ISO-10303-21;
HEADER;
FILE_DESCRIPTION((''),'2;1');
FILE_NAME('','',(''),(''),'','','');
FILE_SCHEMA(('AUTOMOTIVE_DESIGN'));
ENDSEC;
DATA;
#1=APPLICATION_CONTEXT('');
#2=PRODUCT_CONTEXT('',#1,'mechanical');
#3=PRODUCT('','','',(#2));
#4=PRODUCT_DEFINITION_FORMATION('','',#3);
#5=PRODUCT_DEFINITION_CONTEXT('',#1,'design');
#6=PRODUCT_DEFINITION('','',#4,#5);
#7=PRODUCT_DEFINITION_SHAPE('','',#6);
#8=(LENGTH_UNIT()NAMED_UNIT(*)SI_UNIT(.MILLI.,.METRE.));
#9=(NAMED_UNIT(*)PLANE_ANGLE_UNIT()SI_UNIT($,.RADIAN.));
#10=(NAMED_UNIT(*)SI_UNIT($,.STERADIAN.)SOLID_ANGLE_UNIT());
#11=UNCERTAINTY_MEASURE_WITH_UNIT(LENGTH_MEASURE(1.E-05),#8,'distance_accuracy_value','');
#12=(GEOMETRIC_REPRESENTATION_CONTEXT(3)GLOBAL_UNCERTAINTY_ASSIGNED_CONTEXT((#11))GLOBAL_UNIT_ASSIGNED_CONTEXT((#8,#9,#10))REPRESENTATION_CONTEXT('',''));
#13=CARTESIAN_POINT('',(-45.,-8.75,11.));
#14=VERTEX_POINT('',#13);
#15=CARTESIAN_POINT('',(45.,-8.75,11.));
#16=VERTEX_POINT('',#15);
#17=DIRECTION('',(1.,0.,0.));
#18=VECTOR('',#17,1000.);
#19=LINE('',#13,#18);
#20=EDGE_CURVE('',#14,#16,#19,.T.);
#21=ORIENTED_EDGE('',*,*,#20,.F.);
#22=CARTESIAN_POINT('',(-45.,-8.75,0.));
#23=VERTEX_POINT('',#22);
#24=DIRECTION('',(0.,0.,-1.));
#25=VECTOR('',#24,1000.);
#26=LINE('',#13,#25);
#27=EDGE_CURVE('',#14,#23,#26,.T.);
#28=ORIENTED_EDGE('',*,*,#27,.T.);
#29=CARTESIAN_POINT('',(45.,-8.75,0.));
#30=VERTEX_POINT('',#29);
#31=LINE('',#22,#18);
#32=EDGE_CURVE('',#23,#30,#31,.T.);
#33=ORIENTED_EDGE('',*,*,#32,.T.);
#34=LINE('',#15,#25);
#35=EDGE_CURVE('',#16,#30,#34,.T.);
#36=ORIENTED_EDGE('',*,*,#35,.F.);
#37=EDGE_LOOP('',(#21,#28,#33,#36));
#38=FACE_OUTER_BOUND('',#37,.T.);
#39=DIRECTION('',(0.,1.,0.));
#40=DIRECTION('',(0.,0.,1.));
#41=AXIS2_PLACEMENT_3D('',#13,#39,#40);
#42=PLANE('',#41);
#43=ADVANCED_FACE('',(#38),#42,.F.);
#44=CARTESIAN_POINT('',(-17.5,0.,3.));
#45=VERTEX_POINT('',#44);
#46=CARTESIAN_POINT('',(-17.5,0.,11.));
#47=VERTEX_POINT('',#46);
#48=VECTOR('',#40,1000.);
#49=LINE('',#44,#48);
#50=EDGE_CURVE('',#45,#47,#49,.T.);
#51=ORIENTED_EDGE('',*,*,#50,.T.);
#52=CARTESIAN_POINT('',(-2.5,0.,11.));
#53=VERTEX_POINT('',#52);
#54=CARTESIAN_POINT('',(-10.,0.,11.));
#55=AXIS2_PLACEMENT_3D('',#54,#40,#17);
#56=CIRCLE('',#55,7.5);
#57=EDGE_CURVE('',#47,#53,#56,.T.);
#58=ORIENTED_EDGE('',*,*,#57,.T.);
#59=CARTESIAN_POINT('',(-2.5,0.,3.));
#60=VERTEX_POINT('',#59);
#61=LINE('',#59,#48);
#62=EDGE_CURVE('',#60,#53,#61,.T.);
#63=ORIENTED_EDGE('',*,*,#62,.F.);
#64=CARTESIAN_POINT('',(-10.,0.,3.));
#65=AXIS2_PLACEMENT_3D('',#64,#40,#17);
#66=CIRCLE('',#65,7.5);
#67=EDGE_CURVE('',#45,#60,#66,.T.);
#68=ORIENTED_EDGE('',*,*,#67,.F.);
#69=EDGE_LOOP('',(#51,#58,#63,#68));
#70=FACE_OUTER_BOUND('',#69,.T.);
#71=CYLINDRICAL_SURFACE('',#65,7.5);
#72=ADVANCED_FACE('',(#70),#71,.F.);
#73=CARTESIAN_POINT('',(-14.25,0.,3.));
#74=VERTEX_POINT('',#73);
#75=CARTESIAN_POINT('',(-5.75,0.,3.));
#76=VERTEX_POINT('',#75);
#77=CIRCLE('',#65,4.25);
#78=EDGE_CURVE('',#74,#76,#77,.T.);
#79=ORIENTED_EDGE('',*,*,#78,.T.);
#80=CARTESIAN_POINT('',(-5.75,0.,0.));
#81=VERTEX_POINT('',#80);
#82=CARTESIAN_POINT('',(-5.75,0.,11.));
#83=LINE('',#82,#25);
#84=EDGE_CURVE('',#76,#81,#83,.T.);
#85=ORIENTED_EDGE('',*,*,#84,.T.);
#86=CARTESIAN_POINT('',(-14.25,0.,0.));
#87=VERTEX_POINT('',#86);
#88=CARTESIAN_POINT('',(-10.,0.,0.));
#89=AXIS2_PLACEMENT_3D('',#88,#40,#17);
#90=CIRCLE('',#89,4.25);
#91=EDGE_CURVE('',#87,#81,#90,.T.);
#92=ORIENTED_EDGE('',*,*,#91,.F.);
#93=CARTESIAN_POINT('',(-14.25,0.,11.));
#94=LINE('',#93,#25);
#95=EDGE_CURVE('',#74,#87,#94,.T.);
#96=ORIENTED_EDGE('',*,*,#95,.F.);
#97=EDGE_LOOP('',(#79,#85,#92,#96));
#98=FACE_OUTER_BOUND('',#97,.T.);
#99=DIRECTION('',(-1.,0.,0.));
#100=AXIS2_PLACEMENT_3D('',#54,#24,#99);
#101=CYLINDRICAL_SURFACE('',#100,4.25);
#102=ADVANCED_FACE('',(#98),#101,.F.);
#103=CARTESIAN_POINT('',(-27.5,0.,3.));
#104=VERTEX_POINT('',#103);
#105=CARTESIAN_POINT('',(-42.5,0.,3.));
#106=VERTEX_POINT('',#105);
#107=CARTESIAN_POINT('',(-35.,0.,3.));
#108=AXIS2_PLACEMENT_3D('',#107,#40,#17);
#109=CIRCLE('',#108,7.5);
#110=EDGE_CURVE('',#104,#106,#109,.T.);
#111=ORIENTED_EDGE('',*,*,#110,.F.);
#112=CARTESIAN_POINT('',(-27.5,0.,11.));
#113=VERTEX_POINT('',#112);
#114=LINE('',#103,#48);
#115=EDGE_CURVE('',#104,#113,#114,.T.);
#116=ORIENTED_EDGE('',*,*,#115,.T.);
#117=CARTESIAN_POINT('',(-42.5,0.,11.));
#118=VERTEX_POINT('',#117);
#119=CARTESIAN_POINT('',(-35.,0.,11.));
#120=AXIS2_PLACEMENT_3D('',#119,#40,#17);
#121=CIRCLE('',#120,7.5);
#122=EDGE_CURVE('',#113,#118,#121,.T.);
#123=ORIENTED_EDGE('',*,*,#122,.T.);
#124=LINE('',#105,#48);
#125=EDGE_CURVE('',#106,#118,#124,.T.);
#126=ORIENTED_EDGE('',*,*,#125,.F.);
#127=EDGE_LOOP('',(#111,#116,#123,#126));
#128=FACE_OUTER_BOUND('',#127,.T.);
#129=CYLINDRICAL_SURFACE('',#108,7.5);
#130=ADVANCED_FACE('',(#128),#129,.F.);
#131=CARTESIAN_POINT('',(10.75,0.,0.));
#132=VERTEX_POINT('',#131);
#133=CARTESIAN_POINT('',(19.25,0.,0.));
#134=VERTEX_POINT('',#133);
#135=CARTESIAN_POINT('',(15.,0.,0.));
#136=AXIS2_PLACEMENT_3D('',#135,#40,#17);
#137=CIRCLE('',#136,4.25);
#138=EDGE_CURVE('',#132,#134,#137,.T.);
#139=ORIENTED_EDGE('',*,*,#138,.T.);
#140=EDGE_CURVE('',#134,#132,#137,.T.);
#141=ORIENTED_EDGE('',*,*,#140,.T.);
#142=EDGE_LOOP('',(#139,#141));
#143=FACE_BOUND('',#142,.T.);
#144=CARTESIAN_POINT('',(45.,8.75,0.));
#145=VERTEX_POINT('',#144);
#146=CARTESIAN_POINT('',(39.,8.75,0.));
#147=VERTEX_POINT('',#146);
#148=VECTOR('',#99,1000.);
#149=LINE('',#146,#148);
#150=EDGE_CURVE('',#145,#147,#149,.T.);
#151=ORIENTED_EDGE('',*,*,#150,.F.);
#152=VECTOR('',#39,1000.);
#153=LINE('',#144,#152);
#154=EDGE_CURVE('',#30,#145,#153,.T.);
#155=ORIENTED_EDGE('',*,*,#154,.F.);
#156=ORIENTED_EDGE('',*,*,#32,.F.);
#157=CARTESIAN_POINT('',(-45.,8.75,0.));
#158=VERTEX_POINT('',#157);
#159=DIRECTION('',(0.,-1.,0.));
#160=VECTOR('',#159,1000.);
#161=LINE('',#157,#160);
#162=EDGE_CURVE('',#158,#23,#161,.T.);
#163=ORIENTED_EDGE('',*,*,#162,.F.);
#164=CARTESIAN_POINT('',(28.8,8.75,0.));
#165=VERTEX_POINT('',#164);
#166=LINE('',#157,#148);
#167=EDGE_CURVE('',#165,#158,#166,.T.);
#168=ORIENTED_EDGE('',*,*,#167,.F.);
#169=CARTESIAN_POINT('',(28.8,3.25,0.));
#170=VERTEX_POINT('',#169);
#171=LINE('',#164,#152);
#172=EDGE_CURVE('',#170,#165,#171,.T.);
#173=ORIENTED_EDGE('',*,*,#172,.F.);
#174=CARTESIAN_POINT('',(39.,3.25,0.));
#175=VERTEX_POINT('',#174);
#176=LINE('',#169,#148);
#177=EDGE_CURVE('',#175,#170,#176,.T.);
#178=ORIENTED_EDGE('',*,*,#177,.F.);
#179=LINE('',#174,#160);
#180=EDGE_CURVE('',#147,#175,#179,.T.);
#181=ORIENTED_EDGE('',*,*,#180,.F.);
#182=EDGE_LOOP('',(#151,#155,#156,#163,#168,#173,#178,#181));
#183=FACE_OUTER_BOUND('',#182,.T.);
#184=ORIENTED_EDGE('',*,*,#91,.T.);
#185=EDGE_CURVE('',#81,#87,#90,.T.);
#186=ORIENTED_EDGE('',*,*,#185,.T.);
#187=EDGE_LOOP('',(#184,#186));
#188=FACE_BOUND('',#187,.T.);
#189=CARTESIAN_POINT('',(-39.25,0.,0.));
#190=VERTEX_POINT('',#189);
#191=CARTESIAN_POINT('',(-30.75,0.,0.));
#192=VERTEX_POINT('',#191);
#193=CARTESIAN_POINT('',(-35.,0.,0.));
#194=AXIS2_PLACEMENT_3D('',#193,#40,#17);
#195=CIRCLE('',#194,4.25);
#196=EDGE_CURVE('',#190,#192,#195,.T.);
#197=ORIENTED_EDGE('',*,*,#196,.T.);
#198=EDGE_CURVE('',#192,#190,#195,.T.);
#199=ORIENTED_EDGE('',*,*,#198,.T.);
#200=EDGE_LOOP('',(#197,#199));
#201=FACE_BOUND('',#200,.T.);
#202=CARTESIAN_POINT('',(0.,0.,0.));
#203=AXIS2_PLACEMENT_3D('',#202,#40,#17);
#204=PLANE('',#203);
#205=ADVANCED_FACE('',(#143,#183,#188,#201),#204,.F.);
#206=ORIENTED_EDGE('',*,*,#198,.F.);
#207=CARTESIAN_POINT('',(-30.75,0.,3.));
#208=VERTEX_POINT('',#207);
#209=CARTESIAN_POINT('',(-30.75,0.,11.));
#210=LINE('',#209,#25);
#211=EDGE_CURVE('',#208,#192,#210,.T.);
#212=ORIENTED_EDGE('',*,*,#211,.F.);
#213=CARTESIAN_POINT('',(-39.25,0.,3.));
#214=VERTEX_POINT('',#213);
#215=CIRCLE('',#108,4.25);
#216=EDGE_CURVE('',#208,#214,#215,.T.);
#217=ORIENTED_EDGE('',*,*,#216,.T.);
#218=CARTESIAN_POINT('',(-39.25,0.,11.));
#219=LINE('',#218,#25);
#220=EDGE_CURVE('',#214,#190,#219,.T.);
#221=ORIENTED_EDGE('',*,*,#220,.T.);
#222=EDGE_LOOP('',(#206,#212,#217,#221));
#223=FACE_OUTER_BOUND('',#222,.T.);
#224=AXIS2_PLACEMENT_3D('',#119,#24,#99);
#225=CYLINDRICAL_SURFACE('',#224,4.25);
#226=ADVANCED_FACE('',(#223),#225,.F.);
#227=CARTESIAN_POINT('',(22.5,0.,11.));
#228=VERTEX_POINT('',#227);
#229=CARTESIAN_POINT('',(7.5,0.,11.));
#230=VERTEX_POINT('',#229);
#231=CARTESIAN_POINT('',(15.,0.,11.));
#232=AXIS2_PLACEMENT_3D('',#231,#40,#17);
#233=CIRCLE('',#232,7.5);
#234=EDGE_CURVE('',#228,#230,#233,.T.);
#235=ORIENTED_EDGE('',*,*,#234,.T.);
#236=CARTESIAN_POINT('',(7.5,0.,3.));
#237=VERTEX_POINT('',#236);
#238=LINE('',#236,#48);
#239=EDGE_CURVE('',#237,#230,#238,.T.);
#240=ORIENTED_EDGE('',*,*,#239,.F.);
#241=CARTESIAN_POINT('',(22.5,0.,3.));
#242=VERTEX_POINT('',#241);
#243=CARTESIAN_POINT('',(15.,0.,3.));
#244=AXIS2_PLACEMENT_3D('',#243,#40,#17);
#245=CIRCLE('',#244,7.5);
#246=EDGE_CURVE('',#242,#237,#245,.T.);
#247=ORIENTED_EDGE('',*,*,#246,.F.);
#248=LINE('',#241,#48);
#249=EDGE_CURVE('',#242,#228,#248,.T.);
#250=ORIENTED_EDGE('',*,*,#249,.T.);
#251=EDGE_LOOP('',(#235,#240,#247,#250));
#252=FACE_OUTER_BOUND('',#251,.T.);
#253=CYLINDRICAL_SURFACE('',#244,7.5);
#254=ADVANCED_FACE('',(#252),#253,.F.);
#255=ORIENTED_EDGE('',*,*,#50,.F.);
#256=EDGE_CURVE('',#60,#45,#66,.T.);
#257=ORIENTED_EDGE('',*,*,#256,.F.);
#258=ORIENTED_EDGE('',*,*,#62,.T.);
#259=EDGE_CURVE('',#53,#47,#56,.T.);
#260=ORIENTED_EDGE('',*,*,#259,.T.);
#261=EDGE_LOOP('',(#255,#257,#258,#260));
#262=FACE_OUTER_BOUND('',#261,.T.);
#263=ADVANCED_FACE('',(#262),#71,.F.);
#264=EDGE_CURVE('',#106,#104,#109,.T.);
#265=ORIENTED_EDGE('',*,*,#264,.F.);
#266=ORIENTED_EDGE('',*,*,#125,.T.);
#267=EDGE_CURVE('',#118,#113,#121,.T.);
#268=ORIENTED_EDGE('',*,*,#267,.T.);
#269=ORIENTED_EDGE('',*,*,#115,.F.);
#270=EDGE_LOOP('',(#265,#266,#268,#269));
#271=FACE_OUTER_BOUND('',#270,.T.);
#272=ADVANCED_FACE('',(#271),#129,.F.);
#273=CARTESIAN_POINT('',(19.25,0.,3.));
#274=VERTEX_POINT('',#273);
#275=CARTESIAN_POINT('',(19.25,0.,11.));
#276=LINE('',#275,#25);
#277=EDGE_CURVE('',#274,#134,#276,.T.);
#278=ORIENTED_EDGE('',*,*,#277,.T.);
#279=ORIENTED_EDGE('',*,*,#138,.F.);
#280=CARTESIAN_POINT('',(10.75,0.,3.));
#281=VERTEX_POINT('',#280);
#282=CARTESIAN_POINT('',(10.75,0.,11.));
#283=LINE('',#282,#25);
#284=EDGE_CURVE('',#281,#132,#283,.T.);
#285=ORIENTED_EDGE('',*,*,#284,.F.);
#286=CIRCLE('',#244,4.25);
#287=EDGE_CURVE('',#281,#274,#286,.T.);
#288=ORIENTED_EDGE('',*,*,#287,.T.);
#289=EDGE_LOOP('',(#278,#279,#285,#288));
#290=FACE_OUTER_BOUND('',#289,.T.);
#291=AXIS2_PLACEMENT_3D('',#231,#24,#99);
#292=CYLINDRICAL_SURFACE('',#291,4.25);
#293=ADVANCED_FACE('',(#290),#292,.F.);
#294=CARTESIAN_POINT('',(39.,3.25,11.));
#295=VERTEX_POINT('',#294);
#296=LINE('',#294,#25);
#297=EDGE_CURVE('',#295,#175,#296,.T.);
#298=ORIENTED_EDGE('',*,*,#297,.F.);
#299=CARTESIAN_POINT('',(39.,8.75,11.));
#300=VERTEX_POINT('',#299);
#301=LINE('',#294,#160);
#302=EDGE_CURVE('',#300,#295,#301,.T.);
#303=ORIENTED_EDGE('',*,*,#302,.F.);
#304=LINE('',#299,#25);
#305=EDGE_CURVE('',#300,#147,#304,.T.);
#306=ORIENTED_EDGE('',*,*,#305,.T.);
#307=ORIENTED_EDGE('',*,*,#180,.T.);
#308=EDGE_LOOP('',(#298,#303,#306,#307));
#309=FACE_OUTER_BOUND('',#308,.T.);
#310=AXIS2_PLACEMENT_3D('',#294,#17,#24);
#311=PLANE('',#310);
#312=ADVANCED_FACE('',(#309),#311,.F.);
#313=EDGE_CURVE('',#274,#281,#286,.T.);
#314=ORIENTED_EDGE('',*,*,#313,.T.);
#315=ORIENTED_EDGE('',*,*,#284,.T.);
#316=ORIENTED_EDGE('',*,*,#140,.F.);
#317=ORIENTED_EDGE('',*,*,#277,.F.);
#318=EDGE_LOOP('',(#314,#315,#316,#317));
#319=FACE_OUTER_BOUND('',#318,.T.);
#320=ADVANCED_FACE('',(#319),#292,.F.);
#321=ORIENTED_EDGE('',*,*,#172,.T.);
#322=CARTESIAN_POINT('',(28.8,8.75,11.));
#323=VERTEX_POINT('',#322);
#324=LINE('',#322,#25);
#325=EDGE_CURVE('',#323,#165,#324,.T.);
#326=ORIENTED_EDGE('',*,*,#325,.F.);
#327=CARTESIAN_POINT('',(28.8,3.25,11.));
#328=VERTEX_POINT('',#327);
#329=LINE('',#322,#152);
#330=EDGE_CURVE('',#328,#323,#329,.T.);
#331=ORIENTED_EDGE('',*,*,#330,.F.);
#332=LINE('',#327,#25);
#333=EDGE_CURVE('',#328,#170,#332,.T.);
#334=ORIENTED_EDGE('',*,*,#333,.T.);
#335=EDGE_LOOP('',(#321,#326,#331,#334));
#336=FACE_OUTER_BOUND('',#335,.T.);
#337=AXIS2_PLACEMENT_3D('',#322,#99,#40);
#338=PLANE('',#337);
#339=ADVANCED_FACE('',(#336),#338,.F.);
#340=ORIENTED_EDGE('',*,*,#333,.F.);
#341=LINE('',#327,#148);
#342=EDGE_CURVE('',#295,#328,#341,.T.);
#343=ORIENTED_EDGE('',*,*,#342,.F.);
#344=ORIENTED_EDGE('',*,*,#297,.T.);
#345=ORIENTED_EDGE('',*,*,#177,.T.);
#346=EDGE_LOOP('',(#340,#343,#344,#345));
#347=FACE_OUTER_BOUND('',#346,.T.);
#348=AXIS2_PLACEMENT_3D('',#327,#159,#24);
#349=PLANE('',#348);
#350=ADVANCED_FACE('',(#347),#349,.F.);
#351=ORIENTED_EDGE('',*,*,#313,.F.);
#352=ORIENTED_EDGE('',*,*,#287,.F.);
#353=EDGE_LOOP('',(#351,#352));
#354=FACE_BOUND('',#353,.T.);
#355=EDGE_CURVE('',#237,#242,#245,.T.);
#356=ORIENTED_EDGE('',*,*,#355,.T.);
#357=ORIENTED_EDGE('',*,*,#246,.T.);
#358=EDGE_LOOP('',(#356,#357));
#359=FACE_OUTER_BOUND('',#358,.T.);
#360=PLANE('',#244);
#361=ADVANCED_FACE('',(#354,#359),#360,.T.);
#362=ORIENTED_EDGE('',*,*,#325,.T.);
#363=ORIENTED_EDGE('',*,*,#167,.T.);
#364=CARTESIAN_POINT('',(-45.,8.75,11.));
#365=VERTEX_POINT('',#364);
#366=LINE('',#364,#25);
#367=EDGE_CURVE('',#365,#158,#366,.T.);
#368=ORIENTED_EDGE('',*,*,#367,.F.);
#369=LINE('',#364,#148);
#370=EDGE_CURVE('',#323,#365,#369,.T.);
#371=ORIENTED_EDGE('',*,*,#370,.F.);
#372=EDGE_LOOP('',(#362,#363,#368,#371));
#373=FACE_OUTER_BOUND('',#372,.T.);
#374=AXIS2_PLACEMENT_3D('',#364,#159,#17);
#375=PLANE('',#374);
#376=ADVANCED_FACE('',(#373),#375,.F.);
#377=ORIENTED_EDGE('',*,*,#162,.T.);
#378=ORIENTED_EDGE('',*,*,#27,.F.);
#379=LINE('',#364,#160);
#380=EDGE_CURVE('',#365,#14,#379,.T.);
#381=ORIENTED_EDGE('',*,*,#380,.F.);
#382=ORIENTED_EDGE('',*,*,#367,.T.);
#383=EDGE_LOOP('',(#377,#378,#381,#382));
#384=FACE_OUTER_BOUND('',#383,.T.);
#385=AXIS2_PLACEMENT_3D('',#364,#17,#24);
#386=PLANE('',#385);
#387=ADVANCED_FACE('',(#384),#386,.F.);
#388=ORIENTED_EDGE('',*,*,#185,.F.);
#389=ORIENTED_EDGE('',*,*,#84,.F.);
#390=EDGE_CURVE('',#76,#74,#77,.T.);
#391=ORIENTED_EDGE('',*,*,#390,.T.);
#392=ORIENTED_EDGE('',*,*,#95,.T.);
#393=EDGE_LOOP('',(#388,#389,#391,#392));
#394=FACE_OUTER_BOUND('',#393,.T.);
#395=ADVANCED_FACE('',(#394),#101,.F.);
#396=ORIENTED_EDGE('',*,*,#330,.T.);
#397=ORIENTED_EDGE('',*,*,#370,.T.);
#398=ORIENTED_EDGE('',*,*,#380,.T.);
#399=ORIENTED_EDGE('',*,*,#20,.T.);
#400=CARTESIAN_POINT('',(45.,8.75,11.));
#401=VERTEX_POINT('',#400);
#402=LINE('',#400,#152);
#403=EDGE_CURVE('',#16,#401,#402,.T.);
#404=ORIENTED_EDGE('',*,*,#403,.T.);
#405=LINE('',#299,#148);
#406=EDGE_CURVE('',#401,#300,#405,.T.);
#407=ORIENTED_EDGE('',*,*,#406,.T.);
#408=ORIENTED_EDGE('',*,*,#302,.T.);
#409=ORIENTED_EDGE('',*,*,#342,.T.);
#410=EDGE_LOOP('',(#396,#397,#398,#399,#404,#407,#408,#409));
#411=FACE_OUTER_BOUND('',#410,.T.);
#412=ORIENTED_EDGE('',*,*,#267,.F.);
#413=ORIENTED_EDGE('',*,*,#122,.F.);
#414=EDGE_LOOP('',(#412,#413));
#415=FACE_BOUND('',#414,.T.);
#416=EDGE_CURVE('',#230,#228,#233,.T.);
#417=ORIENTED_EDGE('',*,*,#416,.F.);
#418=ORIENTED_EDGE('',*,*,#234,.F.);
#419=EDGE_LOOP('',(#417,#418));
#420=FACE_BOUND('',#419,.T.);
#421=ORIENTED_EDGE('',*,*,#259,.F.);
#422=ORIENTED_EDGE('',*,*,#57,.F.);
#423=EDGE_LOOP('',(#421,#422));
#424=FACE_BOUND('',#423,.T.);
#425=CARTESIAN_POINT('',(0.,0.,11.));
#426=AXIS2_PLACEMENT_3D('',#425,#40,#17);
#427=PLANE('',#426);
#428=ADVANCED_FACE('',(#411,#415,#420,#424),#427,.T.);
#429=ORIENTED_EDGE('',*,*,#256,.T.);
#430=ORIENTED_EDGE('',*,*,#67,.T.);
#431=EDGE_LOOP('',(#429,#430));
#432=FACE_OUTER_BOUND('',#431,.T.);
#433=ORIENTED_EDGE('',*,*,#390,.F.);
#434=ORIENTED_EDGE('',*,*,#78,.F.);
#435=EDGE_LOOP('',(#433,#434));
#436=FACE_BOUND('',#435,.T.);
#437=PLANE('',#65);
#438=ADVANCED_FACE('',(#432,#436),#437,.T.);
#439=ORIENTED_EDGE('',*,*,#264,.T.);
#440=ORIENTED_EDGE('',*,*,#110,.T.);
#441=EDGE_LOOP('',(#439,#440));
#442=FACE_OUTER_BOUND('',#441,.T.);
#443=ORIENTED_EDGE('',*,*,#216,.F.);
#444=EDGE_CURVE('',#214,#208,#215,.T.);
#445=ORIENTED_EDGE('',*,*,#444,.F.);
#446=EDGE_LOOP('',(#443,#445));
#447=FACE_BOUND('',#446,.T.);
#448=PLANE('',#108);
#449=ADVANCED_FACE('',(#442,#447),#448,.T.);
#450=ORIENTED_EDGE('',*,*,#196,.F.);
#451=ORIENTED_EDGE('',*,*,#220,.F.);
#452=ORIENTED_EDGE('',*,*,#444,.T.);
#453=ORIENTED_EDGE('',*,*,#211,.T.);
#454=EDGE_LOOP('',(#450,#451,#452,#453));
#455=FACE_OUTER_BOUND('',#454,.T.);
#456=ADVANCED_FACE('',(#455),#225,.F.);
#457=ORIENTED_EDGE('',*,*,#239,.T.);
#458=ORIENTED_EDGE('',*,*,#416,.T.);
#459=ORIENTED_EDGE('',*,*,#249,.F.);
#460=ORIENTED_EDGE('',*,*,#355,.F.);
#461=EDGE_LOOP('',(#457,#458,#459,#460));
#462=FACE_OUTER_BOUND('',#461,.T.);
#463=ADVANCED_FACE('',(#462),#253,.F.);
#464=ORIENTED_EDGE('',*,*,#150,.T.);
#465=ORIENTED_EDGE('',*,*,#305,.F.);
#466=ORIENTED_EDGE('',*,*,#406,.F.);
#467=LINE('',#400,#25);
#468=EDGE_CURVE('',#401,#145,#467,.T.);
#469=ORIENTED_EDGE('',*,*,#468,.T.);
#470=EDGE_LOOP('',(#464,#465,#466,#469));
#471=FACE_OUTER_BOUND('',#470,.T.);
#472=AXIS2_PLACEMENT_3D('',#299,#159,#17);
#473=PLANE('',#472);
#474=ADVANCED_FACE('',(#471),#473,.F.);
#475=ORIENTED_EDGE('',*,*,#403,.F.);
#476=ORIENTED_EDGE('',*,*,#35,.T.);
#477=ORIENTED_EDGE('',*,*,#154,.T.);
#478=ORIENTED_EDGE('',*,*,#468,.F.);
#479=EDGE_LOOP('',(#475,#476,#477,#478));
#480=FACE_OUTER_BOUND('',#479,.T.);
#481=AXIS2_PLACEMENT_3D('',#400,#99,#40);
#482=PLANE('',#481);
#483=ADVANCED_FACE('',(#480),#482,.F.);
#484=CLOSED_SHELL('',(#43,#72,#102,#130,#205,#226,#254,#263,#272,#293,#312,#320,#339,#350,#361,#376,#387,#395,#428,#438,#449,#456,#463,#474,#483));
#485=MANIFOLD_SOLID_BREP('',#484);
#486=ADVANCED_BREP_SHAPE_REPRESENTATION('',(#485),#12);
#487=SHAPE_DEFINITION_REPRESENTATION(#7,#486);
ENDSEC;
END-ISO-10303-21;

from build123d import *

# Parameters (mm, degrees)
SKETCH1_R           = 4.25
BOSS_EXTRUDE1_DEPTH = 11
SKETCH2_R           = 7.5
CUT_EXTRUDE1_DEPTH  = 8


with BuildPart() as part:
    # Sketch1 → Boss-Extrude1 (new body)
    with BuildSketch(Plane.XY):
        Polygon((-45, 8.75), (28.8, 8.75), (28.8, 3.25), (39, 3.25), (39, 8.75), (45, 8.75), (45, -8.75), (-45, -8.75), align=None)
        with Locations((-35, 0)):
            Circle(SKETCH1_R, mode=Mode.SUBTRACT)
        with Locations((-10, 0)):
            Circle(SKETCH1_R, mode=Mode.SUBTRACT)
        with Locations((15, 0)):
            Circle(SKETCH1_R, mode=Mode.SUBTRACT)
    extrude(amount=BOSS_EXTRUDE1_DEPTH)

    # Sketch2 → Cut-Extrude1 (cut)
    with BuildSketch(Plane.XY.offset(11)):
        with Locations((-35, 0)):
            Circle(SKETCH2_R)
        with Locations((-10, 0)):
            Circle(SKETCH2_R)
        with Locations((15, 0)):
            Circle(SKETCH2_R)
    extrude(amount=-CUT_EXTRUDE1_DEPTH, mode=Mode.SUBTRACT)


solid = part.part
